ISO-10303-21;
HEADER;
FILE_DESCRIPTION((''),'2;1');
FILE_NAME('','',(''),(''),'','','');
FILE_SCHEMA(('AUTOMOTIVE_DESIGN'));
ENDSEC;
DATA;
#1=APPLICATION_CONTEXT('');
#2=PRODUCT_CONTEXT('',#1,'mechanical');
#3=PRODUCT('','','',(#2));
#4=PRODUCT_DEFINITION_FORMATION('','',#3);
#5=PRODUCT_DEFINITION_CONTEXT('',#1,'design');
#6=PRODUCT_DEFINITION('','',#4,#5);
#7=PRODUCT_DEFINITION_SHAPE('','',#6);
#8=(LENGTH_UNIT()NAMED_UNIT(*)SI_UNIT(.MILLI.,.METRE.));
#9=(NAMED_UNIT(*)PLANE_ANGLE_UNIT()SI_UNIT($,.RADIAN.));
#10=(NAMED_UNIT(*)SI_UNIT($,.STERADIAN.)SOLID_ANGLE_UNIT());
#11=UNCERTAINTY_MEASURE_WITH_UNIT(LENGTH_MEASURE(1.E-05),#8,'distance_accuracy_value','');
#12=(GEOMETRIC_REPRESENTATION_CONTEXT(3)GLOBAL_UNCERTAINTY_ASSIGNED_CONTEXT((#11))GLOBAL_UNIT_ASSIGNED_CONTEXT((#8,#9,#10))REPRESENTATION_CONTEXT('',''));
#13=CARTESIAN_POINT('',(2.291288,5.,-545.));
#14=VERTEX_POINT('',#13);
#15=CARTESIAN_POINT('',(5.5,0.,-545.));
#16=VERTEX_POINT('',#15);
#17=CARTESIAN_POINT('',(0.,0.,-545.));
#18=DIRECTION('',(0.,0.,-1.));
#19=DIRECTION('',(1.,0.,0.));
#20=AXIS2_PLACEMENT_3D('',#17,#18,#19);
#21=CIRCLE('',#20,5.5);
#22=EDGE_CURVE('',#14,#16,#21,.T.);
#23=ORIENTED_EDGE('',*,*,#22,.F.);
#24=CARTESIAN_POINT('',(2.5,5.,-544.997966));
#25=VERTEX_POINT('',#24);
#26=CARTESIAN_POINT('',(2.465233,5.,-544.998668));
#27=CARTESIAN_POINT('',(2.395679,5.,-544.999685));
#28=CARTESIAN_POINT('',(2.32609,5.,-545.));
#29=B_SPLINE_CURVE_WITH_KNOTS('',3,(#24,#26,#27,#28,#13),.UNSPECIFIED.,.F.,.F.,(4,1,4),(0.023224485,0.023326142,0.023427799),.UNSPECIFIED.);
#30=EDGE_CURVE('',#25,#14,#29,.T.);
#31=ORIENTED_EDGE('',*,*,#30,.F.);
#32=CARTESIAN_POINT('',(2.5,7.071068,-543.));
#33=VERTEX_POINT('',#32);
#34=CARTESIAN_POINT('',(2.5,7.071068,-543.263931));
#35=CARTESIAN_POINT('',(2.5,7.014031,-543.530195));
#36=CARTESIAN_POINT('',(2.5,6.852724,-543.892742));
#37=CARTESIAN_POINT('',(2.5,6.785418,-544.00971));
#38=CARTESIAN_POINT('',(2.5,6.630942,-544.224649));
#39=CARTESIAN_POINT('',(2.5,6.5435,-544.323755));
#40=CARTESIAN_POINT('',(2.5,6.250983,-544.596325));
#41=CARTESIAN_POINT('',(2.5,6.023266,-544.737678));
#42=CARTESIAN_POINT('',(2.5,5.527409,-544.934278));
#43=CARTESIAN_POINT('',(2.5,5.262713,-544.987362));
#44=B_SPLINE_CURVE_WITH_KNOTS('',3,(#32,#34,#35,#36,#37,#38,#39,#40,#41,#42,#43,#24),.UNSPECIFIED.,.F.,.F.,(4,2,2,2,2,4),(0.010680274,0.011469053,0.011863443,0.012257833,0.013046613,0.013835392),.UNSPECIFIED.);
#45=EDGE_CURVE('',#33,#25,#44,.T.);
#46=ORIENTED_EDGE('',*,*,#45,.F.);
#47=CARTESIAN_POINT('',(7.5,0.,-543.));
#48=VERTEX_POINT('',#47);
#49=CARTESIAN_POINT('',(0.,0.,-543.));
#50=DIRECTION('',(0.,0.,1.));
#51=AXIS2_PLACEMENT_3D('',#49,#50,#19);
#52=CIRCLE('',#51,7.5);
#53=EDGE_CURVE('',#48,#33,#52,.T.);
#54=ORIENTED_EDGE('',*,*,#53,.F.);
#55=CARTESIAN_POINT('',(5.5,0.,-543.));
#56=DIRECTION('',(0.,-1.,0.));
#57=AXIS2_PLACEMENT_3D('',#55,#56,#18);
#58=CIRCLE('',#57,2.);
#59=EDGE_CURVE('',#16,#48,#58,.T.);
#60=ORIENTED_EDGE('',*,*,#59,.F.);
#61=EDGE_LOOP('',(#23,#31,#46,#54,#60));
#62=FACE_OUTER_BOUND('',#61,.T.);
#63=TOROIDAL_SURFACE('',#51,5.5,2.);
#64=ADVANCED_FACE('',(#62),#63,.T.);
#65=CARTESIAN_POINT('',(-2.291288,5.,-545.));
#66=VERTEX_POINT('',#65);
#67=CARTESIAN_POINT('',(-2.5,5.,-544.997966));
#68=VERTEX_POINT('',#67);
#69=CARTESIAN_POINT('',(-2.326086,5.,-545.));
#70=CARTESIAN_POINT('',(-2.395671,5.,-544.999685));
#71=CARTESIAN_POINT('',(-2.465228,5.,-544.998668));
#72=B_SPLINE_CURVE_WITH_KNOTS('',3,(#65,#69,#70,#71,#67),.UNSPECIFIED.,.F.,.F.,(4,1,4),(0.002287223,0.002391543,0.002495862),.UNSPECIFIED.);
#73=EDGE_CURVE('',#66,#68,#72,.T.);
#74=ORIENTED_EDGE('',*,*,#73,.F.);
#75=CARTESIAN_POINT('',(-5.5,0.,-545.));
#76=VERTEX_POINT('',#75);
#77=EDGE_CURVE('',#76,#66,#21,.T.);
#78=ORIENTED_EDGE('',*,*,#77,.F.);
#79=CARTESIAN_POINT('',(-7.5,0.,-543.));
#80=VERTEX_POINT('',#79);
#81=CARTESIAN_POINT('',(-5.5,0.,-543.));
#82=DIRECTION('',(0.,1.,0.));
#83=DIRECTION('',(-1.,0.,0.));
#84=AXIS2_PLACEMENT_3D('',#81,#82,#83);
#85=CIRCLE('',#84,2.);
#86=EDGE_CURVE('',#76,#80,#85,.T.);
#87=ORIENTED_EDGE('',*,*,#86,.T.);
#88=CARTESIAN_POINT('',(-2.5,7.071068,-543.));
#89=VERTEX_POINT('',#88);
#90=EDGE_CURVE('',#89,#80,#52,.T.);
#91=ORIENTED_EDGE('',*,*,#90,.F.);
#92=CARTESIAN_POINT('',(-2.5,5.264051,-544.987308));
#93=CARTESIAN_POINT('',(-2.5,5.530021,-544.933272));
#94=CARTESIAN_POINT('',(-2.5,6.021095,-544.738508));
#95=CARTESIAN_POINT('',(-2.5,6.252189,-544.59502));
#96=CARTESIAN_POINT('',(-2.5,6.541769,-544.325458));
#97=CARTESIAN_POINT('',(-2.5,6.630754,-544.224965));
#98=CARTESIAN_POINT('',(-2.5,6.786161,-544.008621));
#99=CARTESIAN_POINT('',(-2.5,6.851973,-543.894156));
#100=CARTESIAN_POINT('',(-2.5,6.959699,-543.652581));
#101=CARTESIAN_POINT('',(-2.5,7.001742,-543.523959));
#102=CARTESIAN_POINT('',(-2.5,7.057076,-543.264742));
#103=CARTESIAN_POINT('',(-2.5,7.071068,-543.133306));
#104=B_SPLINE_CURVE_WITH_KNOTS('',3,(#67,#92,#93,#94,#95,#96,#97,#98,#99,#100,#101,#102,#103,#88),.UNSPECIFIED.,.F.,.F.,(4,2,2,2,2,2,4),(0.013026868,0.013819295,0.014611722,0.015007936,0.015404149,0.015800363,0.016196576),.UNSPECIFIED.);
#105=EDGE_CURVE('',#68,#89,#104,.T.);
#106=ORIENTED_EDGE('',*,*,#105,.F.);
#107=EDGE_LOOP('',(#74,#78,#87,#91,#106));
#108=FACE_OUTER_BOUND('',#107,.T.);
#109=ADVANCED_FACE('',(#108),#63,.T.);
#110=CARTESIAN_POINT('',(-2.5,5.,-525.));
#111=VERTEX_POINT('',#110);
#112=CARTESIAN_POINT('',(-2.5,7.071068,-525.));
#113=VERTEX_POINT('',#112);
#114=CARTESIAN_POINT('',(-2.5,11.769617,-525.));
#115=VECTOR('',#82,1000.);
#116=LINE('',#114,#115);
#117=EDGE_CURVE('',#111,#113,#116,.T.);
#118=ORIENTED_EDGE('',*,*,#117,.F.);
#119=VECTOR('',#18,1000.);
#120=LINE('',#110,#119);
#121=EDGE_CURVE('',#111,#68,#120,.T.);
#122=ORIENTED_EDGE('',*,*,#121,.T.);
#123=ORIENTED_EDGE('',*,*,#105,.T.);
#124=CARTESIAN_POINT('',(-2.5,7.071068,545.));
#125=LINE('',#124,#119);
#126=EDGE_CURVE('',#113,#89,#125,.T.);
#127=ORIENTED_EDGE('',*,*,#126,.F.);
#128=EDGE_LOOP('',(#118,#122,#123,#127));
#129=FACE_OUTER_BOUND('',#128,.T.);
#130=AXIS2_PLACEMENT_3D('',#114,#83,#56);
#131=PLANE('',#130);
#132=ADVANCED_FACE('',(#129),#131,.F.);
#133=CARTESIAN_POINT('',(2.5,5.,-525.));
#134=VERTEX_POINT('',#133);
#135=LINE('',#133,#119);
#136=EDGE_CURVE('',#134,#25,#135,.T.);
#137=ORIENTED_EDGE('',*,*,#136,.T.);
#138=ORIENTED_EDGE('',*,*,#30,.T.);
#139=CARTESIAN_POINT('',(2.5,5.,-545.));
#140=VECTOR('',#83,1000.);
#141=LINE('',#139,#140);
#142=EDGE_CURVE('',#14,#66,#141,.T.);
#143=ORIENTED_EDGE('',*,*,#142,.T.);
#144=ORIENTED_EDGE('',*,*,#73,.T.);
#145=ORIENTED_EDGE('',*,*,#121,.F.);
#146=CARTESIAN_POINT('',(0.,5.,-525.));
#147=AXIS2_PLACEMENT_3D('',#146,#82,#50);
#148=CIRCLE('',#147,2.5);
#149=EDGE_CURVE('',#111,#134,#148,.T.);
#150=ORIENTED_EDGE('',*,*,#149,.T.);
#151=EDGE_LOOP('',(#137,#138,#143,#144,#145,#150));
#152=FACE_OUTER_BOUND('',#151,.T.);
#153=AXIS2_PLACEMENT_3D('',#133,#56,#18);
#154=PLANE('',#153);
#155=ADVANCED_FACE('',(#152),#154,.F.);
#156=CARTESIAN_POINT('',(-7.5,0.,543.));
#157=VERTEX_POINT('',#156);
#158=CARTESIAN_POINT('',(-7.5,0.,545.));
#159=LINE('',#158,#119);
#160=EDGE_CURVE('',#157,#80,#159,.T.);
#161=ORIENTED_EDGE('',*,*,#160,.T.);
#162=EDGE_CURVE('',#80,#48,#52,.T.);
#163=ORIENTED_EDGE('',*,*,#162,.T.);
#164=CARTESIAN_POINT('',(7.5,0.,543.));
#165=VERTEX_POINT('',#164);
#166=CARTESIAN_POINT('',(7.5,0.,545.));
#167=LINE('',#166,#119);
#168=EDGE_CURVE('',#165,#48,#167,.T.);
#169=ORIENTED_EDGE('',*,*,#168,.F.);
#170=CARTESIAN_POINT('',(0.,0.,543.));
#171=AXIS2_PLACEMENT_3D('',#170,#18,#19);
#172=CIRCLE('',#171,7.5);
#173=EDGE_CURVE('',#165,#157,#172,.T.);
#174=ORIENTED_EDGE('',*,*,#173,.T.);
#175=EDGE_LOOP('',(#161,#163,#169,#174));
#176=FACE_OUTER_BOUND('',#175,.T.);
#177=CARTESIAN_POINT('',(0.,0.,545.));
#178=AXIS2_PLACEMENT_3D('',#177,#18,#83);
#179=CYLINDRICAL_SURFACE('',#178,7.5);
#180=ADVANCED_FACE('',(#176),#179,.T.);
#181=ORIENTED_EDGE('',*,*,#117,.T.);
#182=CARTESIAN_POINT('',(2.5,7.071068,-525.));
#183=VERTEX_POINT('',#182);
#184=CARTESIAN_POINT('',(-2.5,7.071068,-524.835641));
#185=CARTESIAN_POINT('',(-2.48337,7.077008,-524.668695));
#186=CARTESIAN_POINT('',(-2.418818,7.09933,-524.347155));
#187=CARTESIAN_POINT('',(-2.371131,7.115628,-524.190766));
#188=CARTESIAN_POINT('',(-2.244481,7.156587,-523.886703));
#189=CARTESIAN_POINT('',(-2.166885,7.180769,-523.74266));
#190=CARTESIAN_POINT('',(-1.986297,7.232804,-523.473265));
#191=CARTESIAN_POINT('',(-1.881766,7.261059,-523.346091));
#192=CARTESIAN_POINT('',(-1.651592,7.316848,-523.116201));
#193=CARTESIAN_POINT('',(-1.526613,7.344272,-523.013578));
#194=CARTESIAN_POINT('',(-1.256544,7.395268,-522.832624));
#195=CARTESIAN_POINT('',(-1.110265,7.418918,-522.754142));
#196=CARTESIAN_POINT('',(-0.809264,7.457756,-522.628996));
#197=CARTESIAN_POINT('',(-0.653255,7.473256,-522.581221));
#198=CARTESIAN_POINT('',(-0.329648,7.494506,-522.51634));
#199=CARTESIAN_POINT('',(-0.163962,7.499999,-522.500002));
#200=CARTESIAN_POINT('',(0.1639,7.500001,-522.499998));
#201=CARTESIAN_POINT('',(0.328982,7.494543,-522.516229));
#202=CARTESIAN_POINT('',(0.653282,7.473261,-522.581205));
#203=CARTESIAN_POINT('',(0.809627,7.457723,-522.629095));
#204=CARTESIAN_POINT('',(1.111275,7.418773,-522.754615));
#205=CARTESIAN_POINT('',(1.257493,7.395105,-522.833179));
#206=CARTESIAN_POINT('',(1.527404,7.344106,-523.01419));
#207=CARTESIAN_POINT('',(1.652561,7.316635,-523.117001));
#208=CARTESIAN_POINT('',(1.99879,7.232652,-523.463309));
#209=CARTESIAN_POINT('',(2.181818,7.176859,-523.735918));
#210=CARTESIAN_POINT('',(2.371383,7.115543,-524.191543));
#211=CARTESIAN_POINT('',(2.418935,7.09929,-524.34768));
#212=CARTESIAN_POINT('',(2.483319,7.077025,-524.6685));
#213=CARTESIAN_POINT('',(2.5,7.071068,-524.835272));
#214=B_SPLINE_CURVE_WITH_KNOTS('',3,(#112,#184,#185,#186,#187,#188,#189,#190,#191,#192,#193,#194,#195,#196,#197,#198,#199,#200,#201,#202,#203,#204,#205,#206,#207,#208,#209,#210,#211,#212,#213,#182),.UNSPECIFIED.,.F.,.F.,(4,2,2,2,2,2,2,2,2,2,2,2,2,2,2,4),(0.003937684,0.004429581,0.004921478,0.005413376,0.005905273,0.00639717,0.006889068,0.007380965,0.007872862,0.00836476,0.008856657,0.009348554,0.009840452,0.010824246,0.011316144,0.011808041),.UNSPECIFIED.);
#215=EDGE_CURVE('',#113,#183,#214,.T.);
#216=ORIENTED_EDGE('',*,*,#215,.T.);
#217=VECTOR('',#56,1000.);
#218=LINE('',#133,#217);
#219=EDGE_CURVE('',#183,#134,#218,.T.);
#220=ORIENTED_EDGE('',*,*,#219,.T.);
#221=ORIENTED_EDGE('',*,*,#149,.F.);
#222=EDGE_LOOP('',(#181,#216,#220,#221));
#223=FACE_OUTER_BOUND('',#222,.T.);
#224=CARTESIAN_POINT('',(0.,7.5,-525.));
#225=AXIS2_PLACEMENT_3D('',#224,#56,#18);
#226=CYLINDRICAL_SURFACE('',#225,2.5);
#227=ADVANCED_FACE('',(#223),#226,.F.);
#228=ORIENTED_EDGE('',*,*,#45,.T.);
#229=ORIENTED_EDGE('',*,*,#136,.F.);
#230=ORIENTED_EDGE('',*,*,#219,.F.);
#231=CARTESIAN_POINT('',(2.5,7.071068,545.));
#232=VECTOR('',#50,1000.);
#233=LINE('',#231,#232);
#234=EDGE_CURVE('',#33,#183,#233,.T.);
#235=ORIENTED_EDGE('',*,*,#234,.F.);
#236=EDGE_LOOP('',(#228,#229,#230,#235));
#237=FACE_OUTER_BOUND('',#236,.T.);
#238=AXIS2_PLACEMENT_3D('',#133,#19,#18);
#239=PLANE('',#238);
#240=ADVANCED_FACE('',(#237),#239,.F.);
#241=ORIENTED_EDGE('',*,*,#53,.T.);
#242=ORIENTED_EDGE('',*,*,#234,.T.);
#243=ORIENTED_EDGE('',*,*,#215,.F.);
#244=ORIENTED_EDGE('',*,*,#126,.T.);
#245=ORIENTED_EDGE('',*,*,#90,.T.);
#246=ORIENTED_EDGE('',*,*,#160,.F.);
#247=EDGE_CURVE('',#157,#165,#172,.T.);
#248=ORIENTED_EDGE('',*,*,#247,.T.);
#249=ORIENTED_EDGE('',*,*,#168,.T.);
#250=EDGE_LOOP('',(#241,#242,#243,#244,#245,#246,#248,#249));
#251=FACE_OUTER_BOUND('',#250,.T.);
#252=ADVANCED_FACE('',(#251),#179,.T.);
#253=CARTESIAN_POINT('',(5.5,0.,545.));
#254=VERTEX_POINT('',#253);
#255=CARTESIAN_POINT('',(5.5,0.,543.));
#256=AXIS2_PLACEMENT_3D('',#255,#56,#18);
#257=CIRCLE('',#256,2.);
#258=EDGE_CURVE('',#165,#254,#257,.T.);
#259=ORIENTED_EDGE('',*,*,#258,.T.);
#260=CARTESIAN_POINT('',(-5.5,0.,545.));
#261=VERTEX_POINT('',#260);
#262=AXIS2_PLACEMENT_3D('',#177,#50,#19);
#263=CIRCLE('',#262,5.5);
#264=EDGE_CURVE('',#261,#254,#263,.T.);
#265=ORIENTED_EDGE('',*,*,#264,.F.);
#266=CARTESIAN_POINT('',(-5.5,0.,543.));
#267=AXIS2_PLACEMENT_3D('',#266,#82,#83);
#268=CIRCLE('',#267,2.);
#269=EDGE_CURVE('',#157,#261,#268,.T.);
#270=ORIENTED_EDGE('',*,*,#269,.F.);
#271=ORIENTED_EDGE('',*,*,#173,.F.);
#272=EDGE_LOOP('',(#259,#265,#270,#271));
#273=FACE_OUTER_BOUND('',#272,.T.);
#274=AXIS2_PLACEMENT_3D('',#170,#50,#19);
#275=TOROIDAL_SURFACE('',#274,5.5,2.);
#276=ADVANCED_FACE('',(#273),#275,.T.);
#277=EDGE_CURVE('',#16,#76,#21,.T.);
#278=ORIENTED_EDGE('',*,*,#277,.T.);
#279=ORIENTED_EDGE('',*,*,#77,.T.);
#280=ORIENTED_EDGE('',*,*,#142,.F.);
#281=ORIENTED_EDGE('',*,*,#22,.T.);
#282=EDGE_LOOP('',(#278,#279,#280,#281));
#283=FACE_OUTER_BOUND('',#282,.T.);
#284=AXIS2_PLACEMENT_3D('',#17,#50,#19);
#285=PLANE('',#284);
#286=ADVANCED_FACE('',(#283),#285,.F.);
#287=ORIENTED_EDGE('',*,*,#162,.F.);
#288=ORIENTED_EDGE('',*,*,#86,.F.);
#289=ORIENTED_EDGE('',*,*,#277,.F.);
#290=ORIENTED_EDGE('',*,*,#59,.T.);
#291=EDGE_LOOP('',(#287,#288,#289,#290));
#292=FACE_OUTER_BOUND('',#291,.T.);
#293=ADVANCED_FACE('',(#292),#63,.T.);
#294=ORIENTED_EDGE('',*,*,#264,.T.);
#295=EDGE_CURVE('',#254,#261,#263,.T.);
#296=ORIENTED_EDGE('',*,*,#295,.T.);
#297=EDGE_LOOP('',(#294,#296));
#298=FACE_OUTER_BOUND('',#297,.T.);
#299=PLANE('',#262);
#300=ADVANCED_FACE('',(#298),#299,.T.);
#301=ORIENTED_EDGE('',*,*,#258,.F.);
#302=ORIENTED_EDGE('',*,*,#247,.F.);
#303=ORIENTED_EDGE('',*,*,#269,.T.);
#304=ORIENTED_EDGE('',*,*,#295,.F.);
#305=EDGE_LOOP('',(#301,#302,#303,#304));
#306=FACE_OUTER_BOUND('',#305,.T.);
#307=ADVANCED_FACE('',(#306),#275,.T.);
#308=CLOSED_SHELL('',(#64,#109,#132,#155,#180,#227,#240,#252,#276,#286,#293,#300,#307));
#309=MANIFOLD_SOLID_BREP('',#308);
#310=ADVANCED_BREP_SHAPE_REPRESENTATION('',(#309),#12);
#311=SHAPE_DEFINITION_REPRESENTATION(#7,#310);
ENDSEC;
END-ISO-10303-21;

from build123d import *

# Parameters (mm, degrees)
SKETCH_1_R          = 7.5
EXTRUDE_1_DEPTH     = 545
FILLET_1_R          = 2
SKETCH_2_W          = 5
SKETCH_2_H          = 6.769617338
CUT_EXTRUDE_2_DEPTH = 20
SKETCH_3_R          = 2.5
CUT_EXTRUDE_3_DEPTH = 546.194919376


with BuildPart() as part:
    # 草图1 → 拉伸1 (new, symmetric)
    with BuildSketch(Plane.XY):
        Circle(SKETCH_1_R)
    extrude(amount=EXTRUDE_1_DEPTH, both=True)

    # 圆角1
    fillet_1_edges = [part.edges().sort_by_distance(p)[0] for p in [
        (-7.5, 0, -545),
        (-7.5, 0, 545),
    ]]
    fillet(fillet_1_edges, radius=FILLET_1_R)

    # 草图2 → 拉伸2 (cut)
    with BuildSketch(Plane(origin=(0, 0, -545), x_dir=(-1, 0, 0), z_dir=(0, 0, -1))):
        with Locations((0, 8.384808669)):
            Rectangle(SKETCH_2_W, SKETCH_2_H)
    extrude(amount=-CUT_EXTRUDE_2_DEPTH, mode=Mode.SUBTRACT)

    # 草图3 → 拉伸3 (cut, through all)
    with BuildSketch(Plane(origin=(0, 5, 0), x_dir=(1, 0, 0), z_dir=(0, 1, 0))):
        with Locations((0, 525)):
            Circle(SKETCH_3_R)
    extrude(amount=CUT_EXTRUDE_3_DEPTH, mode=Mode.SUBTRACT)


solid = part.part
